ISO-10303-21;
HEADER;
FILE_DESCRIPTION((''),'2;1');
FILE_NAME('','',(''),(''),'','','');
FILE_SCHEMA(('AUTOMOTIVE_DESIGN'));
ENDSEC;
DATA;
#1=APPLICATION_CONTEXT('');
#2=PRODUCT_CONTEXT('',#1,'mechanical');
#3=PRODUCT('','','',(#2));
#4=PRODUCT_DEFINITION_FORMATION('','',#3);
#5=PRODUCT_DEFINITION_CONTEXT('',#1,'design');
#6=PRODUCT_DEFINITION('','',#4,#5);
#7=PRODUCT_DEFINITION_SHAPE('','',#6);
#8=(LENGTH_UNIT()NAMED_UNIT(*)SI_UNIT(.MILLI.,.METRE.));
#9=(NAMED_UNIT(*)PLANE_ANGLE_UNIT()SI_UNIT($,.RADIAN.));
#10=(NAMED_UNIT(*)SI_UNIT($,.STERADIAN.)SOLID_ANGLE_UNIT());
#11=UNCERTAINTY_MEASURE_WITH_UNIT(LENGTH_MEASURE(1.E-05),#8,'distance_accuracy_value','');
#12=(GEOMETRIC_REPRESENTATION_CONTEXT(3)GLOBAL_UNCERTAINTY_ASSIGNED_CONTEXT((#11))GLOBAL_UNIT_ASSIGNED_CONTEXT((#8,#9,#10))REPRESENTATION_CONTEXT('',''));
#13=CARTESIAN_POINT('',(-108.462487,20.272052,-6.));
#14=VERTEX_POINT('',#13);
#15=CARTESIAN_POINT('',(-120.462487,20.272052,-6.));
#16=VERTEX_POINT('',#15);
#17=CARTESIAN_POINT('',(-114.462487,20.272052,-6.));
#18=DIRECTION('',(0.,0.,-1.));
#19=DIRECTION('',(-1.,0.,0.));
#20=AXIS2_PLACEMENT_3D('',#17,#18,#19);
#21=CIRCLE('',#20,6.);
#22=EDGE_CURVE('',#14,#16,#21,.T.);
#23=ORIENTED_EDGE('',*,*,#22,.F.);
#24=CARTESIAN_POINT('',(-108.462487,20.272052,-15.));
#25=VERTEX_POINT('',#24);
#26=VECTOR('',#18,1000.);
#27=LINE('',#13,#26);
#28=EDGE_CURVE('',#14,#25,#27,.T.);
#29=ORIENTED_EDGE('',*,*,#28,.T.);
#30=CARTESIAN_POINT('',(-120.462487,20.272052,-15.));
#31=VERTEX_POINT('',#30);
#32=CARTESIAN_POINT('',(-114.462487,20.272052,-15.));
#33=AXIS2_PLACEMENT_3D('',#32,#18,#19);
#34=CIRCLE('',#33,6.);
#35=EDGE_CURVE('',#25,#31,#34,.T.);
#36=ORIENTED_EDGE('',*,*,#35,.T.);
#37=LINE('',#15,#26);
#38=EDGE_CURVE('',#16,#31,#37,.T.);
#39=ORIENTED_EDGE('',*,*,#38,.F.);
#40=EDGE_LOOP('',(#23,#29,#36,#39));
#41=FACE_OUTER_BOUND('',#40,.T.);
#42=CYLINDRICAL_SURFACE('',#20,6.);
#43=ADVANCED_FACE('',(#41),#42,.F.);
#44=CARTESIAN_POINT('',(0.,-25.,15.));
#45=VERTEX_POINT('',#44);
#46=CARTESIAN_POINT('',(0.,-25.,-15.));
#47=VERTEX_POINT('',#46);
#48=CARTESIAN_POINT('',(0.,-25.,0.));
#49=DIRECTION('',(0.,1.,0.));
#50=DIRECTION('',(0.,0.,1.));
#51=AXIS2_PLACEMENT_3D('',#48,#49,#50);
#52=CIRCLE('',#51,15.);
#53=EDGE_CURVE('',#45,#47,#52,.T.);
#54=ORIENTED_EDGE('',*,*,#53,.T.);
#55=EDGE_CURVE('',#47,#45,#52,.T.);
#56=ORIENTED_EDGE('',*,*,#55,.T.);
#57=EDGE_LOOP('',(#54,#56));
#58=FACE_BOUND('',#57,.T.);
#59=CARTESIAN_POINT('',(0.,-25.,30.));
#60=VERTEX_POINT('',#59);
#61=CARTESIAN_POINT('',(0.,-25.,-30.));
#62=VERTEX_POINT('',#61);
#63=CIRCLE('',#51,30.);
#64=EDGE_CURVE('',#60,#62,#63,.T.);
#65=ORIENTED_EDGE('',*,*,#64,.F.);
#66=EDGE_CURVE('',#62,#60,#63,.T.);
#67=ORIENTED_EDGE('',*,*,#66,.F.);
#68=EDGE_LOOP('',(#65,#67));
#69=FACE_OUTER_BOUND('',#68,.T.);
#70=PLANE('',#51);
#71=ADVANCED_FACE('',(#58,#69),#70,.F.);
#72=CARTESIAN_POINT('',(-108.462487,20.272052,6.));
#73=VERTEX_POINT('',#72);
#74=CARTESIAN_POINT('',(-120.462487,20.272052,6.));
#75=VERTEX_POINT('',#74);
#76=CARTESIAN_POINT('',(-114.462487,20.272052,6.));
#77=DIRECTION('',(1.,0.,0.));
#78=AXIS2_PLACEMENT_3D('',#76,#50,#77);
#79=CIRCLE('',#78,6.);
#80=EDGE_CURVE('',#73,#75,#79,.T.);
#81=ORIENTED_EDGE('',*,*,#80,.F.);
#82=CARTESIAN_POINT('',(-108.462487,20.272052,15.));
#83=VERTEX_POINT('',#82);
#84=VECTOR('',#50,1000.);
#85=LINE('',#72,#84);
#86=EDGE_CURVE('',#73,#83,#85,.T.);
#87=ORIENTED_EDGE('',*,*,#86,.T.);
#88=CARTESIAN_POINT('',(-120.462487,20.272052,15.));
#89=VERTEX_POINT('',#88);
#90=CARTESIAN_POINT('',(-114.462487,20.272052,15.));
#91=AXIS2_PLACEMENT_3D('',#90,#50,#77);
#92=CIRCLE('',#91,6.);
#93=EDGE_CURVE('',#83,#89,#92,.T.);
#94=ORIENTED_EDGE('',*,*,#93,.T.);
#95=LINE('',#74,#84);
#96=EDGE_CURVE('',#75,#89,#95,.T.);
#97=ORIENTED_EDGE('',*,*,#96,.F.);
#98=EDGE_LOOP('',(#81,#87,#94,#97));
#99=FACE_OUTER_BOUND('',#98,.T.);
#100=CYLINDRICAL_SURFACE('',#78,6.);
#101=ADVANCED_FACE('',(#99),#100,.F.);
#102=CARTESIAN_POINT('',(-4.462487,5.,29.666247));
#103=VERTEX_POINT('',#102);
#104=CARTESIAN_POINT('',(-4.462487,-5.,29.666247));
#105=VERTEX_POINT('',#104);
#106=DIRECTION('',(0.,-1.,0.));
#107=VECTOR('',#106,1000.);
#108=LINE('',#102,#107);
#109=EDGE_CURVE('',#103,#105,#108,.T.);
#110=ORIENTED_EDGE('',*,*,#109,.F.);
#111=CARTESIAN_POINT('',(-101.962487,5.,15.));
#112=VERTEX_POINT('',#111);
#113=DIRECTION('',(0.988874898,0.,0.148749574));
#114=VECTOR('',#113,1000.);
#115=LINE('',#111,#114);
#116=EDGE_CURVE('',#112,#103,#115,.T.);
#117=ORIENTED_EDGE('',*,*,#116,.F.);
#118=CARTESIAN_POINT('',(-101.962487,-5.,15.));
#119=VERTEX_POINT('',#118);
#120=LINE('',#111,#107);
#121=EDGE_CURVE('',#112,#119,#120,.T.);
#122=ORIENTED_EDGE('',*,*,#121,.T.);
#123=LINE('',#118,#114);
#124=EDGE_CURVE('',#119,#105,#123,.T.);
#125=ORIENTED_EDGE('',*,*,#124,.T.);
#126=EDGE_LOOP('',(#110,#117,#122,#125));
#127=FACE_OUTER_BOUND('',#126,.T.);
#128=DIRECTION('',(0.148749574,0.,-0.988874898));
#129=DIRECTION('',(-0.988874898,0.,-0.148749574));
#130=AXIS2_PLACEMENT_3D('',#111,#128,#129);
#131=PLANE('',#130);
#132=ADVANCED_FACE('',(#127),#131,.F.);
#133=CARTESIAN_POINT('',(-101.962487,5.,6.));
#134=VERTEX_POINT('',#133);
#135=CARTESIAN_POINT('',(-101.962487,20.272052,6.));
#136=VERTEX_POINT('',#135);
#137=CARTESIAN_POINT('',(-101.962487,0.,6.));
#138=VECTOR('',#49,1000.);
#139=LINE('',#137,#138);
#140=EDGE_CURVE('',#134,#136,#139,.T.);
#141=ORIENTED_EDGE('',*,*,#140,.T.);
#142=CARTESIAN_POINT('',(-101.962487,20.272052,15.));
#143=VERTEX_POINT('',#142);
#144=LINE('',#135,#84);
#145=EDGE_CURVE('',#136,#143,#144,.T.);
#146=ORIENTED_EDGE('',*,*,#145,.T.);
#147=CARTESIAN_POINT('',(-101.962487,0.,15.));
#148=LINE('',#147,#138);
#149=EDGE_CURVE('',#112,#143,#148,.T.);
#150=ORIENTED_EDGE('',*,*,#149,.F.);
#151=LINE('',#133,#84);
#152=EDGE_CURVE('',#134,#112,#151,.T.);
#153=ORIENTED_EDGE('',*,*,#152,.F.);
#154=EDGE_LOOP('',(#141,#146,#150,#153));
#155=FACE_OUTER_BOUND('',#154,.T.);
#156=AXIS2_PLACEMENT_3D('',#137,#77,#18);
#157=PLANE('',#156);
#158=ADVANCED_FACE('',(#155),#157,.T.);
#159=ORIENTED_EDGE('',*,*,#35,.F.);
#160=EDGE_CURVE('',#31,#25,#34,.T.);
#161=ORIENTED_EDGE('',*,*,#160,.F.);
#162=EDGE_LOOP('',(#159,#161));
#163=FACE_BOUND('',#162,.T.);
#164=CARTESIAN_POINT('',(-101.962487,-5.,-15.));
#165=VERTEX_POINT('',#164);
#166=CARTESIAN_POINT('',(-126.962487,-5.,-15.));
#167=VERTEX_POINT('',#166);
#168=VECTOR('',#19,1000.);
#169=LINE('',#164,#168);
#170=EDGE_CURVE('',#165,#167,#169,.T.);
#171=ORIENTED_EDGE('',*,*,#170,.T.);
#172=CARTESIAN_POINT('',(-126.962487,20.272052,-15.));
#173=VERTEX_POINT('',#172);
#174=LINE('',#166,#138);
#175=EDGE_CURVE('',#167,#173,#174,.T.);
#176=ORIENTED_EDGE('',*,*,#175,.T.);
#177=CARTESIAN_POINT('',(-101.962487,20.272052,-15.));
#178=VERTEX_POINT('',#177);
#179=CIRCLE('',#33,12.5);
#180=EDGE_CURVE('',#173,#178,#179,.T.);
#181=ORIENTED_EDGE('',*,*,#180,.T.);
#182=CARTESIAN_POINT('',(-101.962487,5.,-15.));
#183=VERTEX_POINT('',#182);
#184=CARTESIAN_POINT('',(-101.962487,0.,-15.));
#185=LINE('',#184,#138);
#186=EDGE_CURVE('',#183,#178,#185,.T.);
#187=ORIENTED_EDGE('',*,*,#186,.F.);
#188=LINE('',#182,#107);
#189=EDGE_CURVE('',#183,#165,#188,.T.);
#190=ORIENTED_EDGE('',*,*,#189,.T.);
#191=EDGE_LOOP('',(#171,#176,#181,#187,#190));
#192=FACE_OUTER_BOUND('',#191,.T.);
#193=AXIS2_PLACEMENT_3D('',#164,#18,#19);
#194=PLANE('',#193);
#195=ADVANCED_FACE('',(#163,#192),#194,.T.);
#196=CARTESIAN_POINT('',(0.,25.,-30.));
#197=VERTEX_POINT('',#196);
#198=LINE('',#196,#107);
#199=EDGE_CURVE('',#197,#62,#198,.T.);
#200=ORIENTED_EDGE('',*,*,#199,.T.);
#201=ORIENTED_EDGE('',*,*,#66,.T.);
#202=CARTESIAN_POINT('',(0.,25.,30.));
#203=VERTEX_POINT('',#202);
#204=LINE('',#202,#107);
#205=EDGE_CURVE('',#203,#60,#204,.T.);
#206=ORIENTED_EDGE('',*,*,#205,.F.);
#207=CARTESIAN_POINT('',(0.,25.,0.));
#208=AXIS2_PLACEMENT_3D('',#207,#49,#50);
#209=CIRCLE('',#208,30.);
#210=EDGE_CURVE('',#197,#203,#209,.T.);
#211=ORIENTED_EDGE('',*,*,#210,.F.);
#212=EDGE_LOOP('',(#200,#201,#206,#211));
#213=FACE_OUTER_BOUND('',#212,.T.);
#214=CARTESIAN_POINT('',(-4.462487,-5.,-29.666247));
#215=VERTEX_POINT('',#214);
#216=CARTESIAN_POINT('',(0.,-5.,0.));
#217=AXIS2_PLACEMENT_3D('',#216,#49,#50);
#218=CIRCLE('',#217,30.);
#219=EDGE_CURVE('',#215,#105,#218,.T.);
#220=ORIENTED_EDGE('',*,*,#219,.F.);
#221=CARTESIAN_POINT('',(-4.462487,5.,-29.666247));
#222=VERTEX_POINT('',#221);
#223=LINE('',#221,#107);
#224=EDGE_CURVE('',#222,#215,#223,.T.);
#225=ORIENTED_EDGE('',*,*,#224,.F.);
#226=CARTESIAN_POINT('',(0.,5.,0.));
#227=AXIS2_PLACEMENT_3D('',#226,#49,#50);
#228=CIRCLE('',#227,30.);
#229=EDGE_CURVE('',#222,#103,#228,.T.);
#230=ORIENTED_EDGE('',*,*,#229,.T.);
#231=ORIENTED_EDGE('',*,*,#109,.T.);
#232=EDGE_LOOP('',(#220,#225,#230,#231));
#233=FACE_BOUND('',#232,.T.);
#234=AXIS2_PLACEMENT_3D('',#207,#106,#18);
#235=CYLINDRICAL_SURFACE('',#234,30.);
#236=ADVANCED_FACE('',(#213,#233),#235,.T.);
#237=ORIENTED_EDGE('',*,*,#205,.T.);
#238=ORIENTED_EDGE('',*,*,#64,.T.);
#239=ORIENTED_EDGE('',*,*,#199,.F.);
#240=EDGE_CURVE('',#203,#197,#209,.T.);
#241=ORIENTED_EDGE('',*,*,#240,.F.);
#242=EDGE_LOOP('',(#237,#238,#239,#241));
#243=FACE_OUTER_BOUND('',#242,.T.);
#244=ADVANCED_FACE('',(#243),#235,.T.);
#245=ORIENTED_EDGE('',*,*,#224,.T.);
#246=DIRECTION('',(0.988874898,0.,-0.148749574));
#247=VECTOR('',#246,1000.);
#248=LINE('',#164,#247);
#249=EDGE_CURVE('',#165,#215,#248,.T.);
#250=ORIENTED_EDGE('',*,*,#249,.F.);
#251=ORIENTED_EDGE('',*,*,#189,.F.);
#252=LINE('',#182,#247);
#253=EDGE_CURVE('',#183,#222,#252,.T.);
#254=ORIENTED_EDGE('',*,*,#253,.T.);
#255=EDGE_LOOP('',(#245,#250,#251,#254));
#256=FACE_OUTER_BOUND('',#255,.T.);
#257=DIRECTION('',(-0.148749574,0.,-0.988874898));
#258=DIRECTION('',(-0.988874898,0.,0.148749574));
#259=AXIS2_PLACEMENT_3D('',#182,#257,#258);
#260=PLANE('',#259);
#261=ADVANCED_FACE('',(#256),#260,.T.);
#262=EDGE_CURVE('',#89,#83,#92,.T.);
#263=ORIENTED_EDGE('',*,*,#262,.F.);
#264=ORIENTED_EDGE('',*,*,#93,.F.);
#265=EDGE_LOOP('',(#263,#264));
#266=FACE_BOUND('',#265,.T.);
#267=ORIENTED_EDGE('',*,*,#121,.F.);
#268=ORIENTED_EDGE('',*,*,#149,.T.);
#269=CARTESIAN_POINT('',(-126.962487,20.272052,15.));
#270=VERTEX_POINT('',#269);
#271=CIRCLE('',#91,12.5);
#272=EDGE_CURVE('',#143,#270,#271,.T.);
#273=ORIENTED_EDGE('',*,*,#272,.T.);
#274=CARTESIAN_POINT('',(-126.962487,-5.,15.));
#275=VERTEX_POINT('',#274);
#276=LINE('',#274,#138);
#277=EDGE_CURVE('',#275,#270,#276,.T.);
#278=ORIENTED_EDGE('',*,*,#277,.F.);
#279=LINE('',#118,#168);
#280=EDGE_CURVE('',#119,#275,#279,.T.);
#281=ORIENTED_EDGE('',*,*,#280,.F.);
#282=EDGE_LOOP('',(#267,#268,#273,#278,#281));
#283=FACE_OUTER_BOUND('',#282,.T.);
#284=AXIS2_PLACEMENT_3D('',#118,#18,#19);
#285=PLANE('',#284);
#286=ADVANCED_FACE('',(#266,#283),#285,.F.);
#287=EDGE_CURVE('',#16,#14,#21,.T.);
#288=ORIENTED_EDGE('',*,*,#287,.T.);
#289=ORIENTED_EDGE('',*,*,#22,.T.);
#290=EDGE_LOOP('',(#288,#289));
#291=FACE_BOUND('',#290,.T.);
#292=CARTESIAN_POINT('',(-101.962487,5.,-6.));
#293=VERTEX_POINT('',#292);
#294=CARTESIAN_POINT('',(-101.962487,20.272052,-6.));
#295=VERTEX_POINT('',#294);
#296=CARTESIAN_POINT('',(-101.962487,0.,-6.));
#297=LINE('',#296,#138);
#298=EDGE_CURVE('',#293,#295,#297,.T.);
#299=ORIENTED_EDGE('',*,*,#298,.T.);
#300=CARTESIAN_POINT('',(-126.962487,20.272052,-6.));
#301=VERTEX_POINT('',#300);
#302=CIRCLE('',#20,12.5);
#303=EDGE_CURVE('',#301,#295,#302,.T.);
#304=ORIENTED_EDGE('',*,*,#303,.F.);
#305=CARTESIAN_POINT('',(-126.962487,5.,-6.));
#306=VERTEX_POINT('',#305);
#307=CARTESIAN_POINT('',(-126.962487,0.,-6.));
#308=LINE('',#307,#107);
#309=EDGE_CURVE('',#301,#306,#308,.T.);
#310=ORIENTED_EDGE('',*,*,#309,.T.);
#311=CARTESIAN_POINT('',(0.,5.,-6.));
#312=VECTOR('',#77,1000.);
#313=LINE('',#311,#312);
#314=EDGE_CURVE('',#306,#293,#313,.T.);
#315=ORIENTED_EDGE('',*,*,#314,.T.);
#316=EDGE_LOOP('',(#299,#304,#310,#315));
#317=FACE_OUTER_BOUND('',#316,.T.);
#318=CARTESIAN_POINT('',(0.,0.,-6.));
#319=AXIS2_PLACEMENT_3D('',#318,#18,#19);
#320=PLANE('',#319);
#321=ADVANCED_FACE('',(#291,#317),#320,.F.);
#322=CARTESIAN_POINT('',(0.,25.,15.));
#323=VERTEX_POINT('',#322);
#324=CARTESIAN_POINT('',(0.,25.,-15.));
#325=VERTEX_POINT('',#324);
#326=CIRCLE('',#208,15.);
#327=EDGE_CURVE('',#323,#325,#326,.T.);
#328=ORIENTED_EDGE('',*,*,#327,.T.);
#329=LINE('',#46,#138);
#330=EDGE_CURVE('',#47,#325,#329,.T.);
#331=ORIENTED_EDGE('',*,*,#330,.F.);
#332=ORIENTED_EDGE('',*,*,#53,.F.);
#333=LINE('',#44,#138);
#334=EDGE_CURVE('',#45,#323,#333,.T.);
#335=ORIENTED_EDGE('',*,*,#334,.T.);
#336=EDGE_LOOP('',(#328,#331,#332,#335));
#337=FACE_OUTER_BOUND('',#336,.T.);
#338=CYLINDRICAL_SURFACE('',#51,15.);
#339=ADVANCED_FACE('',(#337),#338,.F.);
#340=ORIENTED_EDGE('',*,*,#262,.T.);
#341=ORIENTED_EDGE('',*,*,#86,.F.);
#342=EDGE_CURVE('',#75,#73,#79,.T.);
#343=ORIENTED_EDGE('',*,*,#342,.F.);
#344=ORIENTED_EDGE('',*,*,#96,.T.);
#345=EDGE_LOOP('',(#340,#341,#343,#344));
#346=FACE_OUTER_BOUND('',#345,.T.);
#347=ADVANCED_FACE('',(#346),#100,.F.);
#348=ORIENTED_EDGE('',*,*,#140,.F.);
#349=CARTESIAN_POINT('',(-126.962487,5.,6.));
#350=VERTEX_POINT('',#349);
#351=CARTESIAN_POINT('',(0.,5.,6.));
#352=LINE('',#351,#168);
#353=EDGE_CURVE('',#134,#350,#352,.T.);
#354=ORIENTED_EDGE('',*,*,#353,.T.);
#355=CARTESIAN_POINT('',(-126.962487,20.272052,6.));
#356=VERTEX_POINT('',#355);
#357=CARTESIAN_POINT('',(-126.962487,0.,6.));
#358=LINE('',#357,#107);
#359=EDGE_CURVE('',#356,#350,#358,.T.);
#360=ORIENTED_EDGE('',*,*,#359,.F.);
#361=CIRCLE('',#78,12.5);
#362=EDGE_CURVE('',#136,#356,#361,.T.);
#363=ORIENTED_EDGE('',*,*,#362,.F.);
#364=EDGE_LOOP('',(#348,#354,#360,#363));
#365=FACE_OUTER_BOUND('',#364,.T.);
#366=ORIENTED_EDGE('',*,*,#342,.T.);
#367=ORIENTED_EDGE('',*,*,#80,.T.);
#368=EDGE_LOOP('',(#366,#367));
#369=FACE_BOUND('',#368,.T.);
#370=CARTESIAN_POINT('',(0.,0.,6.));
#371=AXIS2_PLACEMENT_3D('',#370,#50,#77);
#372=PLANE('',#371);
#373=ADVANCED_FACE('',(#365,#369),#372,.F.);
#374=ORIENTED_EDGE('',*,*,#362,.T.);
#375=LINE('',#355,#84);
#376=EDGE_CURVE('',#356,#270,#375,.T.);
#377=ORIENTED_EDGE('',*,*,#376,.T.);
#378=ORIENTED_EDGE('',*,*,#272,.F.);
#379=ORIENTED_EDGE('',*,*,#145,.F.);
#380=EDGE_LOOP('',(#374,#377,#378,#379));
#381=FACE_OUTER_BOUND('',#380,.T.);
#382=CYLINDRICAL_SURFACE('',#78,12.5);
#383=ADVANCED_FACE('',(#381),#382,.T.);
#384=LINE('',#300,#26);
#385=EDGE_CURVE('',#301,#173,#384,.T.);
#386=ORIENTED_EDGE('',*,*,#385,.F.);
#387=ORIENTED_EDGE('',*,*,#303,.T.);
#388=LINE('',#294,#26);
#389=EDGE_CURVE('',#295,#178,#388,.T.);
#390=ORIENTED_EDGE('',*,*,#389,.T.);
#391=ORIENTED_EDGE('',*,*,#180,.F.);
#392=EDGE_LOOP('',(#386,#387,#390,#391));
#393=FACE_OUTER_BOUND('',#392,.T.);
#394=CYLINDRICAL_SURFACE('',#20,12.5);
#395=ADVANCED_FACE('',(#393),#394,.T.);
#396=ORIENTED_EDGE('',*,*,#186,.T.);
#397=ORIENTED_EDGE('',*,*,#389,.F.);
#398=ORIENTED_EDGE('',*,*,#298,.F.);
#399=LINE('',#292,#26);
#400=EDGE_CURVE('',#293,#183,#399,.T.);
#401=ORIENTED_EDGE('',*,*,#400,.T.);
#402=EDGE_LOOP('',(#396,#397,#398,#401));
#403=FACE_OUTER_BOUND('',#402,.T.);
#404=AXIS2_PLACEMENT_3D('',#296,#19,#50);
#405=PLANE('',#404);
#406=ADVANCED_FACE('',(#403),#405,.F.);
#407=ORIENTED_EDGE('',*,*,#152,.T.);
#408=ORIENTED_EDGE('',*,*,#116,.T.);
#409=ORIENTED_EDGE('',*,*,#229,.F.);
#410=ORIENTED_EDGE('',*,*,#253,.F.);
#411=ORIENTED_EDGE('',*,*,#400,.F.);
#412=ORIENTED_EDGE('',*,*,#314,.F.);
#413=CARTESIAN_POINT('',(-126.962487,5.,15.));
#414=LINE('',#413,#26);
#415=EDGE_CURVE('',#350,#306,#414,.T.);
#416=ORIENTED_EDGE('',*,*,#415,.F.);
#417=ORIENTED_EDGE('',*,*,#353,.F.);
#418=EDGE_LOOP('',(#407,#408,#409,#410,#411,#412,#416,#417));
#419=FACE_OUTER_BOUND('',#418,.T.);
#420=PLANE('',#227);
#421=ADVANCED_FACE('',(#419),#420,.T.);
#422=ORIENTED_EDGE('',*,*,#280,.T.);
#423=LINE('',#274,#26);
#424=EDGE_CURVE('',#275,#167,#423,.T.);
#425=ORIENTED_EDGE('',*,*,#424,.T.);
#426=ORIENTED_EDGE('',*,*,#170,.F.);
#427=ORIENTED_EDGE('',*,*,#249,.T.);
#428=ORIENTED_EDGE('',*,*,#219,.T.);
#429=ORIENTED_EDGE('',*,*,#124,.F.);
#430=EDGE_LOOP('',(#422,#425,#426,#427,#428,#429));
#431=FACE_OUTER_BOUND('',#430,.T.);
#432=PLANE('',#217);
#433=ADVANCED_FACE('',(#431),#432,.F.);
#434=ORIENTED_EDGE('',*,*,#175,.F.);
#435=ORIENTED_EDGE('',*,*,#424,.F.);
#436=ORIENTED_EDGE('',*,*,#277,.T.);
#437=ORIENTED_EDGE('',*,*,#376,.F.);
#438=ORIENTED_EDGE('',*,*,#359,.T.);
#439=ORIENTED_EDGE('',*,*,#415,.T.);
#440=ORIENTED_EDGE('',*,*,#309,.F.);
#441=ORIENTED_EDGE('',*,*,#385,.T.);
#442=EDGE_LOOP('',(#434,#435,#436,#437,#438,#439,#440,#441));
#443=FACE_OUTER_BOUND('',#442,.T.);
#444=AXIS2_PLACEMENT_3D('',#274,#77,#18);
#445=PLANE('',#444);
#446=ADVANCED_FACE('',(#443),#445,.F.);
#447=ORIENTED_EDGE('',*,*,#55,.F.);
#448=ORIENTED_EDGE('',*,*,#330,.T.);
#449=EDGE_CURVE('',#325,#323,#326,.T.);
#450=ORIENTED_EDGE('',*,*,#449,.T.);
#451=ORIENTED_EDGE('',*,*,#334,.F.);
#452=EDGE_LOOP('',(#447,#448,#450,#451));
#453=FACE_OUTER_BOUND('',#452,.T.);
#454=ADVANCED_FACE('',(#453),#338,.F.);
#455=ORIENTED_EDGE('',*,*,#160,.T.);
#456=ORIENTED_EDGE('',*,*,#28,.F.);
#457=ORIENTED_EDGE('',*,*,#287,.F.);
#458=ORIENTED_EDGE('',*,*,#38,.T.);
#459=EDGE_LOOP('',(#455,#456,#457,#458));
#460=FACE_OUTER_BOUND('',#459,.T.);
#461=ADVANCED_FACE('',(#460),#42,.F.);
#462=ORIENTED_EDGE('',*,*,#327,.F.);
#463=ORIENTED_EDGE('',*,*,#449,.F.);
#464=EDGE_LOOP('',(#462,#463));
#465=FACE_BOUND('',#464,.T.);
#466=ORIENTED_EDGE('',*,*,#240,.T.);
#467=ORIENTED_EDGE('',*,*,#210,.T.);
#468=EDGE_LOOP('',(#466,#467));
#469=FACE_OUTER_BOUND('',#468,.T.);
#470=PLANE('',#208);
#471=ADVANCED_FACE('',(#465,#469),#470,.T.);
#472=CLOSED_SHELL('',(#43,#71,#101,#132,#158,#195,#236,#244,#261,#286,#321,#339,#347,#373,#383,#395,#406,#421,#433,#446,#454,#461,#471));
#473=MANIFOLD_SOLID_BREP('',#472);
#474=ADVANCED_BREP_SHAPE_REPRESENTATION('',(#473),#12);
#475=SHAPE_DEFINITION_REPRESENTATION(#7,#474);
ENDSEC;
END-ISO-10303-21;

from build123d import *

# Parameters (mm, degrees)
HUB_SKETCH_60_R       = 30
HUB_60X50_DEPTH       = 25
BORE_SKETCH_30_R      = 15
HUB_BORE_30_DEPTH     = 66.574385243
ARM_PLATE_10MM_DEPTH  = 5
CLEVIS_BASE_DEPTH     = 10
CLEVIS_LUG_1_SKETCH_R = 6
CLEVIS_LUG_1_DEPTH    = 9
CLEVIS_START          = -9
CLEVIS_LUG_2_SKETCH_R = 6
CLEVIS_LUG_2_DEPTH    = 9


with BuildPart() as part:
    # Hub Sketch Ø60 → Hub Ø60x50 (new, symmetric)
    with BuildSketch(Plane(origin=(0, 0, 0), x_dir=(1, 0, 0), z_dir=(0, 1, 0))):
        with Locations(Location((0, 0, 0), (0, 0, 270))):
            Circle(HUB_SKETCH_60_R)
    extrude(amount=HUB_60X50_DEPTH, both=True)

    # Bore Sketch Ø30 → Hub Bore Ø30 (cut, through all)
    with BuildSketch(Plane(origin=(0, 25, 0), x_dir=(1, 0, 0), z_dir=(0, 1, 0))):
        with Locations(Location((0, 0, 0), (0, 0, 270))):
            Circle(BORE_SKETCH_30_R)
    extrude(amount=-HUB_BORE_30_DEPTH, mode=Mode.SUBTRACT)

    # Arm Plate Sketch → Arm Plate 10mm (add, symmetric)
    with BuildSketch(Plane(origin=(0, 0, 0), x_dir=(1, 0, 0), z_dir=(0, 1, 0))):
        with BuildLine():
            Line((-101.962487217, 15), (-4.462487217, 29.666246946))
            ThreePointArc((-4.462487217, 29.666246946), (-30, 0), (-4.462487217, -29.666246946))
            Line((-4.462487217, -29.666246946), (-101.962487217, -15))
            Line((-101.962487217, -15), (-101.962487217, 15))
        make_face()
    extrude(amount=ARM_PLATE_10MM_DEPTH, both=True)

    # Clevis Base Sketch → Clevis Base (add)
    with BuildSketch(Plane(origin=(0, 5, 0), x_dir=(1, 0, 0), z_dir=(0, 1, 0))):
        with BuildLine():
            Line((-101.962487217, -15), (-126.962487217, -15))
            Line((-126.962487217, -15), (-126.962487217, 15))
            Line((-126.962487217, 15), (-101.962487217, 15))
            Line((-101.962487217, 15), (-4.462487217, 29.666246946))
            ThreePointArc((-4.462487217, 29.666246946), (-30, 0), (-4.462487217, -29.666246946))
            Line((-4.462487217, -29.666246946), (-101.962487217, -15))
        make_face()
    extrude(amount=-CLEVIS_BASE_DEPTH)

    # Clevis Lug 1 Sketch → Clevis Lug 1 (add)
    with BuildSketch(Plane.XY.offset(15)):
        with BuildLine():
            Line((-101.962487217, 5), (-101.962487217, 20.272052395))
            ThreePointArc((-101.962487217, 20.272052395), (-114.462487217, 32.772052395), (-126.962487217, 20.272052395))
            Line((-126.962487217, 20.272052395), (-126.962487217, 5))
            Line((-126.962487217, 5), (-101.962487217, 5))
        make_face()
        with Locations((-114.462487217, 20.272052395)):
            Circle(CLEVIS_LUG_1_SKETCH_R, mode=Mode.SUBTRACT)
    extrude(amount=-CLEVIS_LUG_1_DEPTH)

    # Clevis Lug 2 Sketch → Clevis Lug 2 (add)
    with BuildSketch(Plane(origin=(0, 0, -15), x_dir=(-1, 0, 0), z_dir=(0, 0, -1)).offset(CLEVIS_START)):
        with BuildLine():
            Line((126.962487217, 20.272052395), (126.962487217, 5))
            Line((126.962487217, 5), (101.962487217, 5))
            Line((101.962487217, 5), (101.962487217, 20.272052395))
            ThreePointArc((101.962487217, 20.272052395), (114.462487217, 32.772052395), (126.962487217, 20.272052395))
        make_face()
        with Locations(Location((114.462487217, 20.272052395, 0), (0, 0, 180))):
            Circle(CLEVIS_LUG_2_SKETCH_R, mode=Mode.SUBTRACT)
    extrude(amount=CLEVIS_LUG_2_DEPTH)


solid = part.part
